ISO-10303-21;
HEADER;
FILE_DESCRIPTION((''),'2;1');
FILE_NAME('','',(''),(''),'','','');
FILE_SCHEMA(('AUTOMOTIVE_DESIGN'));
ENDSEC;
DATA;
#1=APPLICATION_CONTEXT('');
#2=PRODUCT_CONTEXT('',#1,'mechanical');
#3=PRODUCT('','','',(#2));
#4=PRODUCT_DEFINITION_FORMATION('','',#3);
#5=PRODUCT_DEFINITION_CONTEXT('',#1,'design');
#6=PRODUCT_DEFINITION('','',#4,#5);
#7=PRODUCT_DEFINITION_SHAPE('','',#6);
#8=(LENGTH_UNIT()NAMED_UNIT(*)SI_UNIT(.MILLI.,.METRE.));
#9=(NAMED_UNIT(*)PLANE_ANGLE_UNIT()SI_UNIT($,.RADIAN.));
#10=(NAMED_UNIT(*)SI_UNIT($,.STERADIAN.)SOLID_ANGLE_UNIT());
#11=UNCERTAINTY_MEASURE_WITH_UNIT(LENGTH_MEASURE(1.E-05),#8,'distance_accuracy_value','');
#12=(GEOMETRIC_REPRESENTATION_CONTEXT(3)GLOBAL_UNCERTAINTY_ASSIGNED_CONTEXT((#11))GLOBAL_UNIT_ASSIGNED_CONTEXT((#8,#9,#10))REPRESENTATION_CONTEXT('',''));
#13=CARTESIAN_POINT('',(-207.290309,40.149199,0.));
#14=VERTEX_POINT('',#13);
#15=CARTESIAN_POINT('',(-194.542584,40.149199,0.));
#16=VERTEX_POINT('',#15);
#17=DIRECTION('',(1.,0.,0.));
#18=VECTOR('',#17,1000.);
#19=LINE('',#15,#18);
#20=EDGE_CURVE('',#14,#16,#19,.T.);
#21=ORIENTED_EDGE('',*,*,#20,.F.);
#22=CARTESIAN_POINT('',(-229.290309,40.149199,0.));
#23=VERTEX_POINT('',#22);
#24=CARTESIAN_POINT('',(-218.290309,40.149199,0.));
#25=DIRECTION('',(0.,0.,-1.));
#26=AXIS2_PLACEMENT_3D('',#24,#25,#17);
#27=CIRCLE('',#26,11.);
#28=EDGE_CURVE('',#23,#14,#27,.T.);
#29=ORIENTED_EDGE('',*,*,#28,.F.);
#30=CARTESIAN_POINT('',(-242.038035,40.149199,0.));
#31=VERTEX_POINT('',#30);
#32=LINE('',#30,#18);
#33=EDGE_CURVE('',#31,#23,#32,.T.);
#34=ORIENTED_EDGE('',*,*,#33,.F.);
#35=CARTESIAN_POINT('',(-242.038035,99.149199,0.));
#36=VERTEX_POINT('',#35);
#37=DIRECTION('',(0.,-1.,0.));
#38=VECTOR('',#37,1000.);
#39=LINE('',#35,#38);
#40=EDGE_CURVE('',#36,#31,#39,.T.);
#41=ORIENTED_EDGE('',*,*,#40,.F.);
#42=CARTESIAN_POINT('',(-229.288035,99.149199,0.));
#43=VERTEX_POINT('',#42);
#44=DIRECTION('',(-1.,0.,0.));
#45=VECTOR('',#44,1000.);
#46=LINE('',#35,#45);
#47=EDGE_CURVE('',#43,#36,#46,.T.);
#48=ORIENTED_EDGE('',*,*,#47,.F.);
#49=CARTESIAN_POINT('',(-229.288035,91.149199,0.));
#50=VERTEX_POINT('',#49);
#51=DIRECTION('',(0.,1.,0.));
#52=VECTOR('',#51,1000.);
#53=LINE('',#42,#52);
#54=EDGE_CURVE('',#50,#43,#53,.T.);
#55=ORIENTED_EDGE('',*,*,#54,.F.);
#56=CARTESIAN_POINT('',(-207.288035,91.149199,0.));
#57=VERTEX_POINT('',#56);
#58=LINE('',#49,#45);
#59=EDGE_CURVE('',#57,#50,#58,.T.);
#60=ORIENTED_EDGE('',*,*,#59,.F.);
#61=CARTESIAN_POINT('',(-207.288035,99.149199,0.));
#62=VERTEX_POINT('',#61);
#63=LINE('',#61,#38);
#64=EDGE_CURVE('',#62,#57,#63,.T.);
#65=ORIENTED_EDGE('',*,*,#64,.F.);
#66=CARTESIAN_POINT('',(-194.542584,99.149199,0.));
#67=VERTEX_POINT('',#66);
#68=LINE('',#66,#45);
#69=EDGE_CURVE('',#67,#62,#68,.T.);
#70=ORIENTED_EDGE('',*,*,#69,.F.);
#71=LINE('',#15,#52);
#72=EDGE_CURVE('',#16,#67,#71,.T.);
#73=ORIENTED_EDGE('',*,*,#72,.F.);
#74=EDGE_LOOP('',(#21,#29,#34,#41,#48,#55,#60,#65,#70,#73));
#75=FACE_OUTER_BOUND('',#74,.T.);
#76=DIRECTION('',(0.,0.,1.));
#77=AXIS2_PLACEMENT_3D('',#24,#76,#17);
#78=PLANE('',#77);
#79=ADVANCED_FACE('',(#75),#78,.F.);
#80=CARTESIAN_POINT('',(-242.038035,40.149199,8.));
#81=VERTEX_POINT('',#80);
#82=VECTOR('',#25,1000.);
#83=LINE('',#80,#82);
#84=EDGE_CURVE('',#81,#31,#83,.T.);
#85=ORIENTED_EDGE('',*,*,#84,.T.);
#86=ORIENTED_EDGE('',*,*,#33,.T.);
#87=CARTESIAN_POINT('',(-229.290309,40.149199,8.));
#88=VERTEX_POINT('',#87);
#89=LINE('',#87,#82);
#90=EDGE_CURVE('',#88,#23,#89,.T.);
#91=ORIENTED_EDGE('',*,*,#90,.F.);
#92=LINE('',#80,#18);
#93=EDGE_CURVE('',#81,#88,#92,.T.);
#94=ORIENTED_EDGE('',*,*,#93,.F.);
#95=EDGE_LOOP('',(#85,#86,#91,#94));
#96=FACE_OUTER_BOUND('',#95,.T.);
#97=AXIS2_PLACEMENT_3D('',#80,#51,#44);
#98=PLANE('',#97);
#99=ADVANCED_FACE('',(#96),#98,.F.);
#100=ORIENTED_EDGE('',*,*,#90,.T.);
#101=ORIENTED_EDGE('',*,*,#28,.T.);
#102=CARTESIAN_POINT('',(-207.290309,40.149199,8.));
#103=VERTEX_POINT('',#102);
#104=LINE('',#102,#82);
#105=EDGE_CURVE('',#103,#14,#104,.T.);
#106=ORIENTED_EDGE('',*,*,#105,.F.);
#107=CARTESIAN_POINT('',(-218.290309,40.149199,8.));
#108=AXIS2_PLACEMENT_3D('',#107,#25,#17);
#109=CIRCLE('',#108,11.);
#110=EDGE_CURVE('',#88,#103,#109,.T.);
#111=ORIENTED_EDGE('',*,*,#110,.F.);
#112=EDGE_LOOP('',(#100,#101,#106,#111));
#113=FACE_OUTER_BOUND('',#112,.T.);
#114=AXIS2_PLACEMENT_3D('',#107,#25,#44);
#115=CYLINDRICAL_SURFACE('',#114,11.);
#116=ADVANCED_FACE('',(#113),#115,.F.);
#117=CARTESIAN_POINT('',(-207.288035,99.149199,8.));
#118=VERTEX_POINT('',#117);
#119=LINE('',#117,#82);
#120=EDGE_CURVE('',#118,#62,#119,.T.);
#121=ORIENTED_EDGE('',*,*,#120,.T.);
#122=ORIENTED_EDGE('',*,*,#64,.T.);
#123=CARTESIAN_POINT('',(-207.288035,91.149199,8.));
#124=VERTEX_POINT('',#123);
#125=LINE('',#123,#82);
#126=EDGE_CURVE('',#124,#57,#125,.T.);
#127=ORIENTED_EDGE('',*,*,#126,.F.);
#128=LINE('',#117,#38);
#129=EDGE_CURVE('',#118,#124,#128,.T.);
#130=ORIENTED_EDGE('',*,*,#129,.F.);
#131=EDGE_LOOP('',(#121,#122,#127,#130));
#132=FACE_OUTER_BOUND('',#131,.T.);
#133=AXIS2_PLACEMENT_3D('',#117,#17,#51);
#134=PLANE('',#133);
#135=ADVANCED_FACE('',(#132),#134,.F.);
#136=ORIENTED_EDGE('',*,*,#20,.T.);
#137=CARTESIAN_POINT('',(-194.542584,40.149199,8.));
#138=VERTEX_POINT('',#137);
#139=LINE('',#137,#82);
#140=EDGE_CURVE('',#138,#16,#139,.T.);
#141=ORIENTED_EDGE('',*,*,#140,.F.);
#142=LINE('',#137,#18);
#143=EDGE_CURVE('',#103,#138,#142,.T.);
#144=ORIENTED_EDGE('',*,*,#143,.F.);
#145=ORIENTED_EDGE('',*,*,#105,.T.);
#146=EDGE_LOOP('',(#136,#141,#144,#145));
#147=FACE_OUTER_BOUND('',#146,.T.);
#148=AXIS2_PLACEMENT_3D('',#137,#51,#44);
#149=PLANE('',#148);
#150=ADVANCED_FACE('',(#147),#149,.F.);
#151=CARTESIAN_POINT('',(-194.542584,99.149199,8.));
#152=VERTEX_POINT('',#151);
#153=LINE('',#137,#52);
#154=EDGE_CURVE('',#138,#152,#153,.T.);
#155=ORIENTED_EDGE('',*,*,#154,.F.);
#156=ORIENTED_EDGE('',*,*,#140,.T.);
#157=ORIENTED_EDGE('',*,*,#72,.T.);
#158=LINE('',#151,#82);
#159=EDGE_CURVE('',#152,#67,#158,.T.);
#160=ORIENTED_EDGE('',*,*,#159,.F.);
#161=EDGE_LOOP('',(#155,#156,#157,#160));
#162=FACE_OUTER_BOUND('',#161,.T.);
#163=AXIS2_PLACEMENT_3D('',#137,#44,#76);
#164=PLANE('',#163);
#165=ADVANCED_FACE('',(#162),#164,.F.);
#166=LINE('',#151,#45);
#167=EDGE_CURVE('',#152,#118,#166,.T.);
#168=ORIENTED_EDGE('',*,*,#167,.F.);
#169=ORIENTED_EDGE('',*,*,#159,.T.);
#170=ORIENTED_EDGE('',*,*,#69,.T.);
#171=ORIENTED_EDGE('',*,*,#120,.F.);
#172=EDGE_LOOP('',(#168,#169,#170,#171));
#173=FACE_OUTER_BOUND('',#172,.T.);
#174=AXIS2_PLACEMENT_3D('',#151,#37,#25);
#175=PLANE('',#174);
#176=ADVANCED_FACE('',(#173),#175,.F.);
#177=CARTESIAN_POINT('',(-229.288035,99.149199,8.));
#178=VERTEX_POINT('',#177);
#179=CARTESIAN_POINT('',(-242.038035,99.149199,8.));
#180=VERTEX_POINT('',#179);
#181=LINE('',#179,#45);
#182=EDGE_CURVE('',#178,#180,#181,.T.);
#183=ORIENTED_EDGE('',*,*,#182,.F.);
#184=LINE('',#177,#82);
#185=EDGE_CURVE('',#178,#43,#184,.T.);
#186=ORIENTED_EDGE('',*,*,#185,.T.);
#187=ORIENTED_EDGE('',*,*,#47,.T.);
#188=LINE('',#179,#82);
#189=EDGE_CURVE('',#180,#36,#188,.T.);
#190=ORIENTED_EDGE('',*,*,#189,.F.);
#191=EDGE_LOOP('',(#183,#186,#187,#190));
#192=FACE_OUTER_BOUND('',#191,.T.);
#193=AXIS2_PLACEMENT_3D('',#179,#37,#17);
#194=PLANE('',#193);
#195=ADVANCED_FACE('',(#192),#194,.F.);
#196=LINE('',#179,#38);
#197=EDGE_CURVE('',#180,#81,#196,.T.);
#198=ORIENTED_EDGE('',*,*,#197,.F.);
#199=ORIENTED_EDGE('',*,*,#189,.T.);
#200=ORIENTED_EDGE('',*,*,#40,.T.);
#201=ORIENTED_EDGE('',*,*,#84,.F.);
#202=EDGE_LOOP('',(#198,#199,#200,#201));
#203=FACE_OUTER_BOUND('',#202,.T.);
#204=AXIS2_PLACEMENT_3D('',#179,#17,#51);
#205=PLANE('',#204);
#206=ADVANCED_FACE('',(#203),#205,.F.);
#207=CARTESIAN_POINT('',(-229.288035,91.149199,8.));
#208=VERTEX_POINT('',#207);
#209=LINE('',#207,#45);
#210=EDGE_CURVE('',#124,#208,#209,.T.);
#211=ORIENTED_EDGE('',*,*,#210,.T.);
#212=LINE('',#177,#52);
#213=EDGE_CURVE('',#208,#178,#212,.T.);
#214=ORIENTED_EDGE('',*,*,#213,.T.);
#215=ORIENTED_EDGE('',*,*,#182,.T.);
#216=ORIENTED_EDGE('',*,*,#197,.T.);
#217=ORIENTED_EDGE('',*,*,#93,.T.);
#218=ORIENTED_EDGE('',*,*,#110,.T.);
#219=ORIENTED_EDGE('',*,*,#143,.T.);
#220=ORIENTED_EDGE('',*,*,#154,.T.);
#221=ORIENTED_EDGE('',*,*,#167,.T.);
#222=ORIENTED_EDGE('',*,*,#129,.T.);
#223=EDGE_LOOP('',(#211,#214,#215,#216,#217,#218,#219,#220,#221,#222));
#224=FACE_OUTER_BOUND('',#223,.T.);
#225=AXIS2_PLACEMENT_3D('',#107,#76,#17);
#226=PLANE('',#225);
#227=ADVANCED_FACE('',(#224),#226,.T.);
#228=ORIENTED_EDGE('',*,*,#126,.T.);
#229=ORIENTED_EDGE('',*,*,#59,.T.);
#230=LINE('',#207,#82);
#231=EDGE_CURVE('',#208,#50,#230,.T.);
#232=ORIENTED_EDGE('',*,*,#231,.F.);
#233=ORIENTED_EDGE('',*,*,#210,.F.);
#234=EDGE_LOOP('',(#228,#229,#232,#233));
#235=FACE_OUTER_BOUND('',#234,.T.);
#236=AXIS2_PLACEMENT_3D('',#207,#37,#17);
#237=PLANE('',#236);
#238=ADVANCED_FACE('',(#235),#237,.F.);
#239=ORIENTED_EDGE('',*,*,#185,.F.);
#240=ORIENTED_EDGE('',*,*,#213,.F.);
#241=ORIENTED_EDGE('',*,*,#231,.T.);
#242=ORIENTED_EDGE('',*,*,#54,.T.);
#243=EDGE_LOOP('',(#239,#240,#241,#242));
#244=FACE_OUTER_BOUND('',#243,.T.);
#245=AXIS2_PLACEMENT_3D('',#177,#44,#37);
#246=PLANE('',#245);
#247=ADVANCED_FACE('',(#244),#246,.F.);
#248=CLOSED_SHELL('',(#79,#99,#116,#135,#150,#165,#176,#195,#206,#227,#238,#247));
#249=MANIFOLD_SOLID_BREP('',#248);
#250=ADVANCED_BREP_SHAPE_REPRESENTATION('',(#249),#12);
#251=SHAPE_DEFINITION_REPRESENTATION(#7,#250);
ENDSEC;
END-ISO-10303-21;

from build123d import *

# Parameters (mm, degrees)
BOSS_EXTRUDE1_DEPTH = 8


with BuildPart() as part:
    # Sketch1 → Boss-Extrude1 (new body)
    with BuildSketch(Plane.XY):
        with BuildLine():
            Line((-194.542584235, 40.149199278), (-207.290309428, 40.149199278))
            ThreePointArc((-207.290309428, 40.149199278), (-218.290309428, 51.149199278), (-229.290309428, 40.149199278))
            Line((-229.290309428, 40.149199278), (-242.038034621, 40.149199278))
            Line((-242.038034621, 40.149199278), (-242.038034621, 99.149199278))
            Line((-242.038034621, 99.149199278), (-229.288034621, 99.149199278))
            Line((-229.288034621, 99.149199278), (-229.288034621, 91.149199278))
            Line((-229.288034621, 91.149199278), (-207.288034621, 91.149199278))
            Line((-207.288034621, 91.149199278), (-207.288034621, 99.149199278))
            Line((-207.288034621, 99.149199278), (-194.542584235, 99.149199278))
            Line((-194.542584235, 99.149199278), (-194.542584235, 40.149199278))
        make_face()
    extrude(amount=BOSS_EXTRUDE1_DEPTH)


solid = part.part
